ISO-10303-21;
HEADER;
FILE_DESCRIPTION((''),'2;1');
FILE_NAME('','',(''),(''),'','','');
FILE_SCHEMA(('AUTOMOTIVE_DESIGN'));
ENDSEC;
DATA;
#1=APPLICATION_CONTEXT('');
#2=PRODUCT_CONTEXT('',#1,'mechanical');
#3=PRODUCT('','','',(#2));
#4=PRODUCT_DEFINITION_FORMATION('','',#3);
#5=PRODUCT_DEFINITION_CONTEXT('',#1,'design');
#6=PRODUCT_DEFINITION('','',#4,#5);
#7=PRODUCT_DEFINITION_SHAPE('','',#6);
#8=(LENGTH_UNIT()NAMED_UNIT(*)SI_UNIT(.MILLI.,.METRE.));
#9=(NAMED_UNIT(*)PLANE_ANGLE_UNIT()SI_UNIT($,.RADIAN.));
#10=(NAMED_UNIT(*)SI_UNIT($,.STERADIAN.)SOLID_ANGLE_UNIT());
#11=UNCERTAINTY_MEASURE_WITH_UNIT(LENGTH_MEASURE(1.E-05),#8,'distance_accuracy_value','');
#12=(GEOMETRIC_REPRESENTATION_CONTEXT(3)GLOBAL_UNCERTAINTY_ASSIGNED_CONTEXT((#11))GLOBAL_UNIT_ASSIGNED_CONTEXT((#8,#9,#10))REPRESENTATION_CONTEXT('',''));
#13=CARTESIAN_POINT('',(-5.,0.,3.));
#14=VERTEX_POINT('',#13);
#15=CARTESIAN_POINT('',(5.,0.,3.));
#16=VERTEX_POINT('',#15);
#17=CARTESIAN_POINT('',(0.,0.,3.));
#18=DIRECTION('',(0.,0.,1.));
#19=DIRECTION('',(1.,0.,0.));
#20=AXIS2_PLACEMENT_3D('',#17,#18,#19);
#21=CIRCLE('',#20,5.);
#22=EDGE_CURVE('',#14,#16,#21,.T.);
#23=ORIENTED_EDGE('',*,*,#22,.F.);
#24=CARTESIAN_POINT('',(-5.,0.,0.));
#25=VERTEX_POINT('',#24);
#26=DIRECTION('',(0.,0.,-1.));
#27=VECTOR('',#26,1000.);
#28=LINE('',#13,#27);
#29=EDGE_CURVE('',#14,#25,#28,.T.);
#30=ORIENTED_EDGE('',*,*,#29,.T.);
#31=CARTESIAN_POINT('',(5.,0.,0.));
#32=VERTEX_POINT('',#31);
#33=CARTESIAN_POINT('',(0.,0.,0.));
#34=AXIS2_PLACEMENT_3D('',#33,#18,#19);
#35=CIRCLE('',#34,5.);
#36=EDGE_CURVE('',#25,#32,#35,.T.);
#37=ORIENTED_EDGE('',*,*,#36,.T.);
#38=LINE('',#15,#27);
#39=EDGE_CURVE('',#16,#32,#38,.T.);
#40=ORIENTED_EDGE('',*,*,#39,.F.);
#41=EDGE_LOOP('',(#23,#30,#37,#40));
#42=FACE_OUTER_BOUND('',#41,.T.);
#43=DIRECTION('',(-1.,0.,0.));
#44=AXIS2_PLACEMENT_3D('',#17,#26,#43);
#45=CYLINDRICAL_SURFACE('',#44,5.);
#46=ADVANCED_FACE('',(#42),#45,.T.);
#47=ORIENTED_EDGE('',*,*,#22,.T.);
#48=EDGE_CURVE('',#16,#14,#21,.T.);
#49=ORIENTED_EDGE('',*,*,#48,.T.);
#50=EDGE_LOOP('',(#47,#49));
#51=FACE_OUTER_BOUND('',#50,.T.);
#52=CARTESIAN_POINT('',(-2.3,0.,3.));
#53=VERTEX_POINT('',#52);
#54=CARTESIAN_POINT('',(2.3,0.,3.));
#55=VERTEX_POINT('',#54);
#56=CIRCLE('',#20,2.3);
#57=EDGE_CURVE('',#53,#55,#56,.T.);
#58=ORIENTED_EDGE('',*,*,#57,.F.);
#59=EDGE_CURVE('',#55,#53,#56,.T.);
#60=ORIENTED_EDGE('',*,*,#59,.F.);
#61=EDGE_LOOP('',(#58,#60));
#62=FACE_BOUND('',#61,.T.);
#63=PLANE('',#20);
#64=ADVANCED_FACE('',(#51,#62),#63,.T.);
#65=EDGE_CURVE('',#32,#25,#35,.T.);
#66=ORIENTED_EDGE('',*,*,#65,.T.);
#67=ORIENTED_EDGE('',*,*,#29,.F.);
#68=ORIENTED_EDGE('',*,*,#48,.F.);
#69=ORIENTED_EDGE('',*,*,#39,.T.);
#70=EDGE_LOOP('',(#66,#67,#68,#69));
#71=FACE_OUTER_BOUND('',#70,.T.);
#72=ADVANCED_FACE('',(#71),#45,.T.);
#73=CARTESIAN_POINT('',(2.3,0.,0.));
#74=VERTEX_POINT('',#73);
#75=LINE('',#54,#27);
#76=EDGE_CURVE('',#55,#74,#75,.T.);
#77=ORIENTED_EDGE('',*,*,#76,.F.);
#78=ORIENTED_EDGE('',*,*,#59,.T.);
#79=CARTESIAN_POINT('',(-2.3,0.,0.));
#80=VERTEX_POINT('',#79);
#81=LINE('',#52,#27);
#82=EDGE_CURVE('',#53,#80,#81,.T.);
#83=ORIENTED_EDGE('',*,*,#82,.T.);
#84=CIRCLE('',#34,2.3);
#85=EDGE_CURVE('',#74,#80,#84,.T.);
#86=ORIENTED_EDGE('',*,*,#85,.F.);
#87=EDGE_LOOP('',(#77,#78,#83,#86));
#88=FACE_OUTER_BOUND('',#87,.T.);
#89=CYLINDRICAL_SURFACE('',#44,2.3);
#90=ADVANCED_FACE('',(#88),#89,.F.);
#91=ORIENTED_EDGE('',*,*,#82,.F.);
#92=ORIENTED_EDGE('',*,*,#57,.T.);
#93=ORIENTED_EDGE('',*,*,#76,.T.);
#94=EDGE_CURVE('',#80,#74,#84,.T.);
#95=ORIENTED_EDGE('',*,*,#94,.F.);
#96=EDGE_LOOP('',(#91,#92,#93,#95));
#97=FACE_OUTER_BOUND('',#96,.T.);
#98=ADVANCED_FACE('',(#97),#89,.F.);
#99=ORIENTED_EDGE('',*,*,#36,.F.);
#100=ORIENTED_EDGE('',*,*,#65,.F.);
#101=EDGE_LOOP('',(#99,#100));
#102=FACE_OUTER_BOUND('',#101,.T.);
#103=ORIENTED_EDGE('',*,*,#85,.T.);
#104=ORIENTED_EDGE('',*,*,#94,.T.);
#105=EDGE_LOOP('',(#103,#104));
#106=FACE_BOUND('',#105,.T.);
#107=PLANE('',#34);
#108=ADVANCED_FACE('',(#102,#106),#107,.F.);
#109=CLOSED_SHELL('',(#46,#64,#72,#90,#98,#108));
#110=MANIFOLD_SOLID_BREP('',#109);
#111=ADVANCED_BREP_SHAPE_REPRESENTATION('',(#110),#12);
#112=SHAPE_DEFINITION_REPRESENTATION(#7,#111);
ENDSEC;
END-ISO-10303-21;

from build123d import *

# Parameters (mm, degrees)
SKETCH1_R           = 5
SKETCH1_R_2         = 2.3
BOSS_EXTRUDE1_DEPTH = 3


with BuildPart() as part:
    # Sketch1 → Boss-Extrude1 (new body)
    with BuildSketch(Plane.XY):
        Circle(SKETCH1_R)
        Circle(SKETCH1_R_2, mode=Mode.SUBTRACT)
    extrude(amount=BOSS_EXTRUDE1_DEPTH)


solid = part.part
